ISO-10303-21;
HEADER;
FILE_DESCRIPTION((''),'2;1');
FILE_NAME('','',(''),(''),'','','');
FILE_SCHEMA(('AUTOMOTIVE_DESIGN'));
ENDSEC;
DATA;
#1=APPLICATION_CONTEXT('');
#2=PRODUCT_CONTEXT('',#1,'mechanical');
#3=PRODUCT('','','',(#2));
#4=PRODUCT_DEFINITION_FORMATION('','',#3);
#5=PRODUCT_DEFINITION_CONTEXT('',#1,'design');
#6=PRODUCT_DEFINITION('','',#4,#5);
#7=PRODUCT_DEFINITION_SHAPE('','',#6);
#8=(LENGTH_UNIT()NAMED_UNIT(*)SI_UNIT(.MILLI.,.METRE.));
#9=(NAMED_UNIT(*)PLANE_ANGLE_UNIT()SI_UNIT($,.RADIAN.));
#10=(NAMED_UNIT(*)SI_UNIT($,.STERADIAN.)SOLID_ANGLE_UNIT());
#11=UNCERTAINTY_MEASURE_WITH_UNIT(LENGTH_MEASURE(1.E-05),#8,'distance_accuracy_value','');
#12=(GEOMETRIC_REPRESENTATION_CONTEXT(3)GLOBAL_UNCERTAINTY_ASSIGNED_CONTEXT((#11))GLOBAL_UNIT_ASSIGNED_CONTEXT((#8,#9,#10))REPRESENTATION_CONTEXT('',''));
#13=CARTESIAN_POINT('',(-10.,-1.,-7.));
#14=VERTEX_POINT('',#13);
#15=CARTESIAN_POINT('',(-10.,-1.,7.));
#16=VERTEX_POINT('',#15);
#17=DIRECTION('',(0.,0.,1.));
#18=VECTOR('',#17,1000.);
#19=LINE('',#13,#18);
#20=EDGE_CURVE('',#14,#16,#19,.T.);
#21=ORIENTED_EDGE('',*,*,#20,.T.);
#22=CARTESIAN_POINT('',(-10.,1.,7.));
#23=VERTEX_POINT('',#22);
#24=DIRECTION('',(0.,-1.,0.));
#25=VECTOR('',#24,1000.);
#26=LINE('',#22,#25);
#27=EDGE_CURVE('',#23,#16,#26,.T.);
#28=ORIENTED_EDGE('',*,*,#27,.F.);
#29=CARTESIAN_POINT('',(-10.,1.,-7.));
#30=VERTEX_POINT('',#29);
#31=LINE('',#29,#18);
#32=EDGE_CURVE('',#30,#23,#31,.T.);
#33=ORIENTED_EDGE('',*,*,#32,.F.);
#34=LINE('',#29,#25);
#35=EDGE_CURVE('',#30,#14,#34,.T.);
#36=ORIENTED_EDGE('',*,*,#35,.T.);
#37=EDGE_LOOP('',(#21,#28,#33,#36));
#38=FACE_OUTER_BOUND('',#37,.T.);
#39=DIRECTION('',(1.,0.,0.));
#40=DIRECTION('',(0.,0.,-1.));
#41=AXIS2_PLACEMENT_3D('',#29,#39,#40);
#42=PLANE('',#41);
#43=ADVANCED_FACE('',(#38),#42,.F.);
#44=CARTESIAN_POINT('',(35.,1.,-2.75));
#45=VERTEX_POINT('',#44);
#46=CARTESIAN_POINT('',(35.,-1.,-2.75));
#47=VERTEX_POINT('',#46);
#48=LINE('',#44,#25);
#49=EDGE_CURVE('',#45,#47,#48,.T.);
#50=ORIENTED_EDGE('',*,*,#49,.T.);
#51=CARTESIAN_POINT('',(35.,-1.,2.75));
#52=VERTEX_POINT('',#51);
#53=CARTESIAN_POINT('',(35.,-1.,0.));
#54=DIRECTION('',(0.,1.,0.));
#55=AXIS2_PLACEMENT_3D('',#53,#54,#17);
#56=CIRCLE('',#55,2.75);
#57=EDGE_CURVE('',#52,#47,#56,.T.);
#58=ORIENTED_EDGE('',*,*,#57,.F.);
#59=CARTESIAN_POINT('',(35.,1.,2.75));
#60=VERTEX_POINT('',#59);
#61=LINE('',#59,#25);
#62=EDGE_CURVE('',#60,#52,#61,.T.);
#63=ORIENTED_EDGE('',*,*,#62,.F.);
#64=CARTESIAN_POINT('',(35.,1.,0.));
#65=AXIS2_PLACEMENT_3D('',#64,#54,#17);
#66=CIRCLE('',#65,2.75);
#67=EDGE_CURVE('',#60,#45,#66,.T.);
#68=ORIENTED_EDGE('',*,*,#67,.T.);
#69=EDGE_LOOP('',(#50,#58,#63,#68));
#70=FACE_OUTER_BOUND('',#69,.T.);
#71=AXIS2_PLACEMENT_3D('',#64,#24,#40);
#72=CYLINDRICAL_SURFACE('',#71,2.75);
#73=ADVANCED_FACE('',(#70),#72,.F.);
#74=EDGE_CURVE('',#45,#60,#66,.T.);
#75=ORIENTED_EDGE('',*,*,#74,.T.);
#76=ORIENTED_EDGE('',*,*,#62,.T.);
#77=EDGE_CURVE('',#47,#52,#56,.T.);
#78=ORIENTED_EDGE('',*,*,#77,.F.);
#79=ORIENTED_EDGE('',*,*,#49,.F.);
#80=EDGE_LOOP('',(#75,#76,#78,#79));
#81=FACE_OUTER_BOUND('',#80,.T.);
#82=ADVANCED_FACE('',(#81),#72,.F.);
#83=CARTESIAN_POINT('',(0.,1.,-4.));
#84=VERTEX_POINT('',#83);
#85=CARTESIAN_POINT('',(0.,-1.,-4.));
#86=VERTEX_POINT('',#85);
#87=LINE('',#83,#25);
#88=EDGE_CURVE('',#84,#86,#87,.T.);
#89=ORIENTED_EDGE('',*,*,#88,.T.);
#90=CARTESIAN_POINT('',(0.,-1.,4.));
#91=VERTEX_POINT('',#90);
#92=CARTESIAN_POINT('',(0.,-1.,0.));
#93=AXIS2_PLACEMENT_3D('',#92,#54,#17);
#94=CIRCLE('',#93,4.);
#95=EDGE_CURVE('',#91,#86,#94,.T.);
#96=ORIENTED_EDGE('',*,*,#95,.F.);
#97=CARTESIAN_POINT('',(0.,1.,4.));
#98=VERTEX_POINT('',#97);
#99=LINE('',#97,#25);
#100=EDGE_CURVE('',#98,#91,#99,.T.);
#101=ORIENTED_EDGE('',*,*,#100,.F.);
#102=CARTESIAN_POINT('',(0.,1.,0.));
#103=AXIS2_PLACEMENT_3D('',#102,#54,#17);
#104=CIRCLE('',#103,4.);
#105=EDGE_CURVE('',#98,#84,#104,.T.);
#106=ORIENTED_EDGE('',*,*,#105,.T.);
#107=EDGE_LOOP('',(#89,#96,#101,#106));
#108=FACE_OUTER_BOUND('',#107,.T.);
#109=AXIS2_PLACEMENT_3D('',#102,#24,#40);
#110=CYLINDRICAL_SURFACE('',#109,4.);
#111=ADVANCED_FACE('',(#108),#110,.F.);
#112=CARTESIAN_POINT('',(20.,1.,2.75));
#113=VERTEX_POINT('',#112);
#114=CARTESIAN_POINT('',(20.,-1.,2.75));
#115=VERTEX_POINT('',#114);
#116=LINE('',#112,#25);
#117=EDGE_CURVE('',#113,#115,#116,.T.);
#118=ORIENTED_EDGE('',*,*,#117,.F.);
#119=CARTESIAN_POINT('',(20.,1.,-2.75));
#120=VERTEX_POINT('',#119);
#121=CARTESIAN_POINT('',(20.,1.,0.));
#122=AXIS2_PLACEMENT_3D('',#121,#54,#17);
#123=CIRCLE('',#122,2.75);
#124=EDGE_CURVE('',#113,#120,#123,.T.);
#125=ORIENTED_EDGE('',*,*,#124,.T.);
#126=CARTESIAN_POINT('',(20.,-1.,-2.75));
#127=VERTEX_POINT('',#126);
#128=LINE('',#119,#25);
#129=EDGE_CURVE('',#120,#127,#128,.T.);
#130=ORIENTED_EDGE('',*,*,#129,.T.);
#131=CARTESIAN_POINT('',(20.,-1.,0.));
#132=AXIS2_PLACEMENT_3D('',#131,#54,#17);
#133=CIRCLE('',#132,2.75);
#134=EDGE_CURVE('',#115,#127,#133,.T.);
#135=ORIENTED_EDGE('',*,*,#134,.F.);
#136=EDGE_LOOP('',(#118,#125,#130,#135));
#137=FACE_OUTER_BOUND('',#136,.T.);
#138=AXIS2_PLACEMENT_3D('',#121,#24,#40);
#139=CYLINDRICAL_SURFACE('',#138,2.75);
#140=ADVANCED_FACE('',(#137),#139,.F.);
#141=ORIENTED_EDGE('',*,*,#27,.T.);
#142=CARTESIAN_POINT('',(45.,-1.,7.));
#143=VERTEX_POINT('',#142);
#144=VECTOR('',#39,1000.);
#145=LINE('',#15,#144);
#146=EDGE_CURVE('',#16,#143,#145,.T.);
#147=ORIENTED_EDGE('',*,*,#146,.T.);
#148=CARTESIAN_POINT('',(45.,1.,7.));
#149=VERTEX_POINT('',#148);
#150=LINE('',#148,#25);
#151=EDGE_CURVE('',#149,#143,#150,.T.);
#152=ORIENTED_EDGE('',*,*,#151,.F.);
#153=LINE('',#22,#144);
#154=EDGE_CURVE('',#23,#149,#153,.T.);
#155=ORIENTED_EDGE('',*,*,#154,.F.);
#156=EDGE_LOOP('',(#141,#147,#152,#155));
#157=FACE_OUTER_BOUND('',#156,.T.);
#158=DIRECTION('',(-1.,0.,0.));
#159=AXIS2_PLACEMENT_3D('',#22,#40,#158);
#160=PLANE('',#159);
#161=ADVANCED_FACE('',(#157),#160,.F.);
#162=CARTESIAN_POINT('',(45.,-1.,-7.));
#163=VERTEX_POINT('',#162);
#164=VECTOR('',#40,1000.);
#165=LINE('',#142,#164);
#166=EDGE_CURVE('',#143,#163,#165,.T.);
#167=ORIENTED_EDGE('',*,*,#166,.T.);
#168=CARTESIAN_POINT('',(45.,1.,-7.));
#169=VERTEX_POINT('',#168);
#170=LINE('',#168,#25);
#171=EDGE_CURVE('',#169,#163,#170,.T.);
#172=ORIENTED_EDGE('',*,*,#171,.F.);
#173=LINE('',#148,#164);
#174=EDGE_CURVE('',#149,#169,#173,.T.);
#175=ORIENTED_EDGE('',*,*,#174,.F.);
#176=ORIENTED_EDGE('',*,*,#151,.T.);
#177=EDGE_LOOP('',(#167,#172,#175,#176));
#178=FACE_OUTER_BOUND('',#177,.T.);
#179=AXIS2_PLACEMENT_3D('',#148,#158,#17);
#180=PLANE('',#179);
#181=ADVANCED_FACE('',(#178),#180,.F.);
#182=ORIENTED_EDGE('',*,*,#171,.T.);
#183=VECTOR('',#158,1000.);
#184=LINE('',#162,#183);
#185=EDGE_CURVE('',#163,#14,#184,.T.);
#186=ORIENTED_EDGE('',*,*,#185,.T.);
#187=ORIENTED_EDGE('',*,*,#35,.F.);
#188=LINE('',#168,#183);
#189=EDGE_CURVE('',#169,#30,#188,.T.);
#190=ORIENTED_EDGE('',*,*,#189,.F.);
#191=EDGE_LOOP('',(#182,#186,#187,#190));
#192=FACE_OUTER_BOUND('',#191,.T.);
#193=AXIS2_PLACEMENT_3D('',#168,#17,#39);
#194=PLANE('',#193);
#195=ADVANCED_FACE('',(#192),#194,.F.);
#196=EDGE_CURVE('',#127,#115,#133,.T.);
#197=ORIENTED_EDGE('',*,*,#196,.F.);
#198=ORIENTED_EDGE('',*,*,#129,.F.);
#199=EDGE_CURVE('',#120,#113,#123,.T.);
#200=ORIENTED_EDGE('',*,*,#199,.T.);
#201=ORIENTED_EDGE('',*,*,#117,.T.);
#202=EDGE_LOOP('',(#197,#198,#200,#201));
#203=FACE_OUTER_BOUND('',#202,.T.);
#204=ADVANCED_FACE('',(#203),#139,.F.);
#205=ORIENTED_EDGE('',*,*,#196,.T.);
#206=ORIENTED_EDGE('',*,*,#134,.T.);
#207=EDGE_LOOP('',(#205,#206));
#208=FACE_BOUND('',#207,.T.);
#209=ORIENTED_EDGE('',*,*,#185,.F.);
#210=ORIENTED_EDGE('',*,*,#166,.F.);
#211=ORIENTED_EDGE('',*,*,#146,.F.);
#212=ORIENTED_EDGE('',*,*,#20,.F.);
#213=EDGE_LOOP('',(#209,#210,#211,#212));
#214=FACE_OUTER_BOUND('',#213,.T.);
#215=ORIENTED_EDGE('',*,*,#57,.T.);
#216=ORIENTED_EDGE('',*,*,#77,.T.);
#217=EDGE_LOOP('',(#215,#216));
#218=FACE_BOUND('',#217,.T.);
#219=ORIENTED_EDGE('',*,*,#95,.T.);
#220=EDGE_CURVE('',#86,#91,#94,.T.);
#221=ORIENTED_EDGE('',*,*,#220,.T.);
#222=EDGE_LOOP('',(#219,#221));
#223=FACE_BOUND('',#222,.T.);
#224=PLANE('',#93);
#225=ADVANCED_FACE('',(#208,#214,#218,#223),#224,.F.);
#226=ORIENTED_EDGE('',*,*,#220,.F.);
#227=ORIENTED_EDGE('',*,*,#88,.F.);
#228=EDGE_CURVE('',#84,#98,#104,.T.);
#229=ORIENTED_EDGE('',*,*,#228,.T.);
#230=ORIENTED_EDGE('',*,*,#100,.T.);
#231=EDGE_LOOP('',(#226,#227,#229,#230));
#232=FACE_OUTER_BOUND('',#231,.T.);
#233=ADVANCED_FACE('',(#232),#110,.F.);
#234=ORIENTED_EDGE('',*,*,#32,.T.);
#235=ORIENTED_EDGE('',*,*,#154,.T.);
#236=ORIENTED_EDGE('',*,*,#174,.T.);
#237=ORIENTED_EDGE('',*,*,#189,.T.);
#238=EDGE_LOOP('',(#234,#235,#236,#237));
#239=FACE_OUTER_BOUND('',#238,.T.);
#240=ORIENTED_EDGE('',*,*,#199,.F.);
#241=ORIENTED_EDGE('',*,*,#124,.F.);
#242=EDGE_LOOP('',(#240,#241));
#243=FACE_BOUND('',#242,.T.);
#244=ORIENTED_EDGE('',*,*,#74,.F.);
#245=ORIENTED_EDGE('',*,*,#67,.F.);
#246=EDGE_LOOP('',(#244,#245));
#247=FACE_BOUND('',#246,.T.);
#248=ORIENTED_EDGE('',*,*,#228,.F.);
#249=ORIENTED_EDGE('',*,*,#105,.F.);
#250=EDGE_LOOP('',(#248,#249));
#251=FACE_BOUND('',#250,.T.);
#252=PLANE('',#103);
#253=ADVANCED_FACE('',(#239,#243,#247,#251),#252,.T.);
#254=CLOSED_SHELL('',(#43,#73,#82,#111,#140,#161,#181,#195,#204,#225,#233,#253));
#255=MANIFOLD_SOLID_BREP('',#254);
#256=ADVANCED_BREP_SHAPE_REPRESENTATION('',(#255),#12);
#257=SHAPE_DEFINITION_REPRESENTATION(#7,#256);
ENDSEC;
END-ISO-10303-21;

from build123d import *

# Parameters (mm, degrees)
EXTRUDE_1_DEPTH      = 1
EXTRUDE_1_DEPTH_BACK = 1
SKETCH_1_W           = 55
SKETCH_1_H           = 14
SKETCH_1_R           = 2.75
SKETCH_1_R_2         = 4


with BuildPart() as part:
    # 草图1 → 凸台-拉伸1 (new, two sides: drawn at the far end of the back side and taken through both)
    with BuildSketch(Plane(origin=(0, 0, 0), x_dir=(1, 0, 0), z_dir=(0, 1, 0)).offset(-EXTRUDE_1_DEPTH_BACK)):
        with Locations((17.5, 0)):
            Rectangle(SKETCH_1_W, SKETCH_1_H)
        with Locations(Location((35, 0, 0), (0, 0, 270))):
            Circle(SKETCH_1_R, mode=Mode.SUBTRACT)
        with Locations(Location((20, 0, 0), (0, 0, 270))):
            Circle(SKETCH_1_R, mode=Mode.SUBTRACT)
        with Locations(Location((0, 0, 0), (0, 0, 270))):
            Circle(SKETCH_1_R_2, mode=Mode.SUBTRACT)
    extrude(amount=EXTRUDE_1_DEPTH + EXTRUDE_1_DEPTH_BACK)


solid = part.part
